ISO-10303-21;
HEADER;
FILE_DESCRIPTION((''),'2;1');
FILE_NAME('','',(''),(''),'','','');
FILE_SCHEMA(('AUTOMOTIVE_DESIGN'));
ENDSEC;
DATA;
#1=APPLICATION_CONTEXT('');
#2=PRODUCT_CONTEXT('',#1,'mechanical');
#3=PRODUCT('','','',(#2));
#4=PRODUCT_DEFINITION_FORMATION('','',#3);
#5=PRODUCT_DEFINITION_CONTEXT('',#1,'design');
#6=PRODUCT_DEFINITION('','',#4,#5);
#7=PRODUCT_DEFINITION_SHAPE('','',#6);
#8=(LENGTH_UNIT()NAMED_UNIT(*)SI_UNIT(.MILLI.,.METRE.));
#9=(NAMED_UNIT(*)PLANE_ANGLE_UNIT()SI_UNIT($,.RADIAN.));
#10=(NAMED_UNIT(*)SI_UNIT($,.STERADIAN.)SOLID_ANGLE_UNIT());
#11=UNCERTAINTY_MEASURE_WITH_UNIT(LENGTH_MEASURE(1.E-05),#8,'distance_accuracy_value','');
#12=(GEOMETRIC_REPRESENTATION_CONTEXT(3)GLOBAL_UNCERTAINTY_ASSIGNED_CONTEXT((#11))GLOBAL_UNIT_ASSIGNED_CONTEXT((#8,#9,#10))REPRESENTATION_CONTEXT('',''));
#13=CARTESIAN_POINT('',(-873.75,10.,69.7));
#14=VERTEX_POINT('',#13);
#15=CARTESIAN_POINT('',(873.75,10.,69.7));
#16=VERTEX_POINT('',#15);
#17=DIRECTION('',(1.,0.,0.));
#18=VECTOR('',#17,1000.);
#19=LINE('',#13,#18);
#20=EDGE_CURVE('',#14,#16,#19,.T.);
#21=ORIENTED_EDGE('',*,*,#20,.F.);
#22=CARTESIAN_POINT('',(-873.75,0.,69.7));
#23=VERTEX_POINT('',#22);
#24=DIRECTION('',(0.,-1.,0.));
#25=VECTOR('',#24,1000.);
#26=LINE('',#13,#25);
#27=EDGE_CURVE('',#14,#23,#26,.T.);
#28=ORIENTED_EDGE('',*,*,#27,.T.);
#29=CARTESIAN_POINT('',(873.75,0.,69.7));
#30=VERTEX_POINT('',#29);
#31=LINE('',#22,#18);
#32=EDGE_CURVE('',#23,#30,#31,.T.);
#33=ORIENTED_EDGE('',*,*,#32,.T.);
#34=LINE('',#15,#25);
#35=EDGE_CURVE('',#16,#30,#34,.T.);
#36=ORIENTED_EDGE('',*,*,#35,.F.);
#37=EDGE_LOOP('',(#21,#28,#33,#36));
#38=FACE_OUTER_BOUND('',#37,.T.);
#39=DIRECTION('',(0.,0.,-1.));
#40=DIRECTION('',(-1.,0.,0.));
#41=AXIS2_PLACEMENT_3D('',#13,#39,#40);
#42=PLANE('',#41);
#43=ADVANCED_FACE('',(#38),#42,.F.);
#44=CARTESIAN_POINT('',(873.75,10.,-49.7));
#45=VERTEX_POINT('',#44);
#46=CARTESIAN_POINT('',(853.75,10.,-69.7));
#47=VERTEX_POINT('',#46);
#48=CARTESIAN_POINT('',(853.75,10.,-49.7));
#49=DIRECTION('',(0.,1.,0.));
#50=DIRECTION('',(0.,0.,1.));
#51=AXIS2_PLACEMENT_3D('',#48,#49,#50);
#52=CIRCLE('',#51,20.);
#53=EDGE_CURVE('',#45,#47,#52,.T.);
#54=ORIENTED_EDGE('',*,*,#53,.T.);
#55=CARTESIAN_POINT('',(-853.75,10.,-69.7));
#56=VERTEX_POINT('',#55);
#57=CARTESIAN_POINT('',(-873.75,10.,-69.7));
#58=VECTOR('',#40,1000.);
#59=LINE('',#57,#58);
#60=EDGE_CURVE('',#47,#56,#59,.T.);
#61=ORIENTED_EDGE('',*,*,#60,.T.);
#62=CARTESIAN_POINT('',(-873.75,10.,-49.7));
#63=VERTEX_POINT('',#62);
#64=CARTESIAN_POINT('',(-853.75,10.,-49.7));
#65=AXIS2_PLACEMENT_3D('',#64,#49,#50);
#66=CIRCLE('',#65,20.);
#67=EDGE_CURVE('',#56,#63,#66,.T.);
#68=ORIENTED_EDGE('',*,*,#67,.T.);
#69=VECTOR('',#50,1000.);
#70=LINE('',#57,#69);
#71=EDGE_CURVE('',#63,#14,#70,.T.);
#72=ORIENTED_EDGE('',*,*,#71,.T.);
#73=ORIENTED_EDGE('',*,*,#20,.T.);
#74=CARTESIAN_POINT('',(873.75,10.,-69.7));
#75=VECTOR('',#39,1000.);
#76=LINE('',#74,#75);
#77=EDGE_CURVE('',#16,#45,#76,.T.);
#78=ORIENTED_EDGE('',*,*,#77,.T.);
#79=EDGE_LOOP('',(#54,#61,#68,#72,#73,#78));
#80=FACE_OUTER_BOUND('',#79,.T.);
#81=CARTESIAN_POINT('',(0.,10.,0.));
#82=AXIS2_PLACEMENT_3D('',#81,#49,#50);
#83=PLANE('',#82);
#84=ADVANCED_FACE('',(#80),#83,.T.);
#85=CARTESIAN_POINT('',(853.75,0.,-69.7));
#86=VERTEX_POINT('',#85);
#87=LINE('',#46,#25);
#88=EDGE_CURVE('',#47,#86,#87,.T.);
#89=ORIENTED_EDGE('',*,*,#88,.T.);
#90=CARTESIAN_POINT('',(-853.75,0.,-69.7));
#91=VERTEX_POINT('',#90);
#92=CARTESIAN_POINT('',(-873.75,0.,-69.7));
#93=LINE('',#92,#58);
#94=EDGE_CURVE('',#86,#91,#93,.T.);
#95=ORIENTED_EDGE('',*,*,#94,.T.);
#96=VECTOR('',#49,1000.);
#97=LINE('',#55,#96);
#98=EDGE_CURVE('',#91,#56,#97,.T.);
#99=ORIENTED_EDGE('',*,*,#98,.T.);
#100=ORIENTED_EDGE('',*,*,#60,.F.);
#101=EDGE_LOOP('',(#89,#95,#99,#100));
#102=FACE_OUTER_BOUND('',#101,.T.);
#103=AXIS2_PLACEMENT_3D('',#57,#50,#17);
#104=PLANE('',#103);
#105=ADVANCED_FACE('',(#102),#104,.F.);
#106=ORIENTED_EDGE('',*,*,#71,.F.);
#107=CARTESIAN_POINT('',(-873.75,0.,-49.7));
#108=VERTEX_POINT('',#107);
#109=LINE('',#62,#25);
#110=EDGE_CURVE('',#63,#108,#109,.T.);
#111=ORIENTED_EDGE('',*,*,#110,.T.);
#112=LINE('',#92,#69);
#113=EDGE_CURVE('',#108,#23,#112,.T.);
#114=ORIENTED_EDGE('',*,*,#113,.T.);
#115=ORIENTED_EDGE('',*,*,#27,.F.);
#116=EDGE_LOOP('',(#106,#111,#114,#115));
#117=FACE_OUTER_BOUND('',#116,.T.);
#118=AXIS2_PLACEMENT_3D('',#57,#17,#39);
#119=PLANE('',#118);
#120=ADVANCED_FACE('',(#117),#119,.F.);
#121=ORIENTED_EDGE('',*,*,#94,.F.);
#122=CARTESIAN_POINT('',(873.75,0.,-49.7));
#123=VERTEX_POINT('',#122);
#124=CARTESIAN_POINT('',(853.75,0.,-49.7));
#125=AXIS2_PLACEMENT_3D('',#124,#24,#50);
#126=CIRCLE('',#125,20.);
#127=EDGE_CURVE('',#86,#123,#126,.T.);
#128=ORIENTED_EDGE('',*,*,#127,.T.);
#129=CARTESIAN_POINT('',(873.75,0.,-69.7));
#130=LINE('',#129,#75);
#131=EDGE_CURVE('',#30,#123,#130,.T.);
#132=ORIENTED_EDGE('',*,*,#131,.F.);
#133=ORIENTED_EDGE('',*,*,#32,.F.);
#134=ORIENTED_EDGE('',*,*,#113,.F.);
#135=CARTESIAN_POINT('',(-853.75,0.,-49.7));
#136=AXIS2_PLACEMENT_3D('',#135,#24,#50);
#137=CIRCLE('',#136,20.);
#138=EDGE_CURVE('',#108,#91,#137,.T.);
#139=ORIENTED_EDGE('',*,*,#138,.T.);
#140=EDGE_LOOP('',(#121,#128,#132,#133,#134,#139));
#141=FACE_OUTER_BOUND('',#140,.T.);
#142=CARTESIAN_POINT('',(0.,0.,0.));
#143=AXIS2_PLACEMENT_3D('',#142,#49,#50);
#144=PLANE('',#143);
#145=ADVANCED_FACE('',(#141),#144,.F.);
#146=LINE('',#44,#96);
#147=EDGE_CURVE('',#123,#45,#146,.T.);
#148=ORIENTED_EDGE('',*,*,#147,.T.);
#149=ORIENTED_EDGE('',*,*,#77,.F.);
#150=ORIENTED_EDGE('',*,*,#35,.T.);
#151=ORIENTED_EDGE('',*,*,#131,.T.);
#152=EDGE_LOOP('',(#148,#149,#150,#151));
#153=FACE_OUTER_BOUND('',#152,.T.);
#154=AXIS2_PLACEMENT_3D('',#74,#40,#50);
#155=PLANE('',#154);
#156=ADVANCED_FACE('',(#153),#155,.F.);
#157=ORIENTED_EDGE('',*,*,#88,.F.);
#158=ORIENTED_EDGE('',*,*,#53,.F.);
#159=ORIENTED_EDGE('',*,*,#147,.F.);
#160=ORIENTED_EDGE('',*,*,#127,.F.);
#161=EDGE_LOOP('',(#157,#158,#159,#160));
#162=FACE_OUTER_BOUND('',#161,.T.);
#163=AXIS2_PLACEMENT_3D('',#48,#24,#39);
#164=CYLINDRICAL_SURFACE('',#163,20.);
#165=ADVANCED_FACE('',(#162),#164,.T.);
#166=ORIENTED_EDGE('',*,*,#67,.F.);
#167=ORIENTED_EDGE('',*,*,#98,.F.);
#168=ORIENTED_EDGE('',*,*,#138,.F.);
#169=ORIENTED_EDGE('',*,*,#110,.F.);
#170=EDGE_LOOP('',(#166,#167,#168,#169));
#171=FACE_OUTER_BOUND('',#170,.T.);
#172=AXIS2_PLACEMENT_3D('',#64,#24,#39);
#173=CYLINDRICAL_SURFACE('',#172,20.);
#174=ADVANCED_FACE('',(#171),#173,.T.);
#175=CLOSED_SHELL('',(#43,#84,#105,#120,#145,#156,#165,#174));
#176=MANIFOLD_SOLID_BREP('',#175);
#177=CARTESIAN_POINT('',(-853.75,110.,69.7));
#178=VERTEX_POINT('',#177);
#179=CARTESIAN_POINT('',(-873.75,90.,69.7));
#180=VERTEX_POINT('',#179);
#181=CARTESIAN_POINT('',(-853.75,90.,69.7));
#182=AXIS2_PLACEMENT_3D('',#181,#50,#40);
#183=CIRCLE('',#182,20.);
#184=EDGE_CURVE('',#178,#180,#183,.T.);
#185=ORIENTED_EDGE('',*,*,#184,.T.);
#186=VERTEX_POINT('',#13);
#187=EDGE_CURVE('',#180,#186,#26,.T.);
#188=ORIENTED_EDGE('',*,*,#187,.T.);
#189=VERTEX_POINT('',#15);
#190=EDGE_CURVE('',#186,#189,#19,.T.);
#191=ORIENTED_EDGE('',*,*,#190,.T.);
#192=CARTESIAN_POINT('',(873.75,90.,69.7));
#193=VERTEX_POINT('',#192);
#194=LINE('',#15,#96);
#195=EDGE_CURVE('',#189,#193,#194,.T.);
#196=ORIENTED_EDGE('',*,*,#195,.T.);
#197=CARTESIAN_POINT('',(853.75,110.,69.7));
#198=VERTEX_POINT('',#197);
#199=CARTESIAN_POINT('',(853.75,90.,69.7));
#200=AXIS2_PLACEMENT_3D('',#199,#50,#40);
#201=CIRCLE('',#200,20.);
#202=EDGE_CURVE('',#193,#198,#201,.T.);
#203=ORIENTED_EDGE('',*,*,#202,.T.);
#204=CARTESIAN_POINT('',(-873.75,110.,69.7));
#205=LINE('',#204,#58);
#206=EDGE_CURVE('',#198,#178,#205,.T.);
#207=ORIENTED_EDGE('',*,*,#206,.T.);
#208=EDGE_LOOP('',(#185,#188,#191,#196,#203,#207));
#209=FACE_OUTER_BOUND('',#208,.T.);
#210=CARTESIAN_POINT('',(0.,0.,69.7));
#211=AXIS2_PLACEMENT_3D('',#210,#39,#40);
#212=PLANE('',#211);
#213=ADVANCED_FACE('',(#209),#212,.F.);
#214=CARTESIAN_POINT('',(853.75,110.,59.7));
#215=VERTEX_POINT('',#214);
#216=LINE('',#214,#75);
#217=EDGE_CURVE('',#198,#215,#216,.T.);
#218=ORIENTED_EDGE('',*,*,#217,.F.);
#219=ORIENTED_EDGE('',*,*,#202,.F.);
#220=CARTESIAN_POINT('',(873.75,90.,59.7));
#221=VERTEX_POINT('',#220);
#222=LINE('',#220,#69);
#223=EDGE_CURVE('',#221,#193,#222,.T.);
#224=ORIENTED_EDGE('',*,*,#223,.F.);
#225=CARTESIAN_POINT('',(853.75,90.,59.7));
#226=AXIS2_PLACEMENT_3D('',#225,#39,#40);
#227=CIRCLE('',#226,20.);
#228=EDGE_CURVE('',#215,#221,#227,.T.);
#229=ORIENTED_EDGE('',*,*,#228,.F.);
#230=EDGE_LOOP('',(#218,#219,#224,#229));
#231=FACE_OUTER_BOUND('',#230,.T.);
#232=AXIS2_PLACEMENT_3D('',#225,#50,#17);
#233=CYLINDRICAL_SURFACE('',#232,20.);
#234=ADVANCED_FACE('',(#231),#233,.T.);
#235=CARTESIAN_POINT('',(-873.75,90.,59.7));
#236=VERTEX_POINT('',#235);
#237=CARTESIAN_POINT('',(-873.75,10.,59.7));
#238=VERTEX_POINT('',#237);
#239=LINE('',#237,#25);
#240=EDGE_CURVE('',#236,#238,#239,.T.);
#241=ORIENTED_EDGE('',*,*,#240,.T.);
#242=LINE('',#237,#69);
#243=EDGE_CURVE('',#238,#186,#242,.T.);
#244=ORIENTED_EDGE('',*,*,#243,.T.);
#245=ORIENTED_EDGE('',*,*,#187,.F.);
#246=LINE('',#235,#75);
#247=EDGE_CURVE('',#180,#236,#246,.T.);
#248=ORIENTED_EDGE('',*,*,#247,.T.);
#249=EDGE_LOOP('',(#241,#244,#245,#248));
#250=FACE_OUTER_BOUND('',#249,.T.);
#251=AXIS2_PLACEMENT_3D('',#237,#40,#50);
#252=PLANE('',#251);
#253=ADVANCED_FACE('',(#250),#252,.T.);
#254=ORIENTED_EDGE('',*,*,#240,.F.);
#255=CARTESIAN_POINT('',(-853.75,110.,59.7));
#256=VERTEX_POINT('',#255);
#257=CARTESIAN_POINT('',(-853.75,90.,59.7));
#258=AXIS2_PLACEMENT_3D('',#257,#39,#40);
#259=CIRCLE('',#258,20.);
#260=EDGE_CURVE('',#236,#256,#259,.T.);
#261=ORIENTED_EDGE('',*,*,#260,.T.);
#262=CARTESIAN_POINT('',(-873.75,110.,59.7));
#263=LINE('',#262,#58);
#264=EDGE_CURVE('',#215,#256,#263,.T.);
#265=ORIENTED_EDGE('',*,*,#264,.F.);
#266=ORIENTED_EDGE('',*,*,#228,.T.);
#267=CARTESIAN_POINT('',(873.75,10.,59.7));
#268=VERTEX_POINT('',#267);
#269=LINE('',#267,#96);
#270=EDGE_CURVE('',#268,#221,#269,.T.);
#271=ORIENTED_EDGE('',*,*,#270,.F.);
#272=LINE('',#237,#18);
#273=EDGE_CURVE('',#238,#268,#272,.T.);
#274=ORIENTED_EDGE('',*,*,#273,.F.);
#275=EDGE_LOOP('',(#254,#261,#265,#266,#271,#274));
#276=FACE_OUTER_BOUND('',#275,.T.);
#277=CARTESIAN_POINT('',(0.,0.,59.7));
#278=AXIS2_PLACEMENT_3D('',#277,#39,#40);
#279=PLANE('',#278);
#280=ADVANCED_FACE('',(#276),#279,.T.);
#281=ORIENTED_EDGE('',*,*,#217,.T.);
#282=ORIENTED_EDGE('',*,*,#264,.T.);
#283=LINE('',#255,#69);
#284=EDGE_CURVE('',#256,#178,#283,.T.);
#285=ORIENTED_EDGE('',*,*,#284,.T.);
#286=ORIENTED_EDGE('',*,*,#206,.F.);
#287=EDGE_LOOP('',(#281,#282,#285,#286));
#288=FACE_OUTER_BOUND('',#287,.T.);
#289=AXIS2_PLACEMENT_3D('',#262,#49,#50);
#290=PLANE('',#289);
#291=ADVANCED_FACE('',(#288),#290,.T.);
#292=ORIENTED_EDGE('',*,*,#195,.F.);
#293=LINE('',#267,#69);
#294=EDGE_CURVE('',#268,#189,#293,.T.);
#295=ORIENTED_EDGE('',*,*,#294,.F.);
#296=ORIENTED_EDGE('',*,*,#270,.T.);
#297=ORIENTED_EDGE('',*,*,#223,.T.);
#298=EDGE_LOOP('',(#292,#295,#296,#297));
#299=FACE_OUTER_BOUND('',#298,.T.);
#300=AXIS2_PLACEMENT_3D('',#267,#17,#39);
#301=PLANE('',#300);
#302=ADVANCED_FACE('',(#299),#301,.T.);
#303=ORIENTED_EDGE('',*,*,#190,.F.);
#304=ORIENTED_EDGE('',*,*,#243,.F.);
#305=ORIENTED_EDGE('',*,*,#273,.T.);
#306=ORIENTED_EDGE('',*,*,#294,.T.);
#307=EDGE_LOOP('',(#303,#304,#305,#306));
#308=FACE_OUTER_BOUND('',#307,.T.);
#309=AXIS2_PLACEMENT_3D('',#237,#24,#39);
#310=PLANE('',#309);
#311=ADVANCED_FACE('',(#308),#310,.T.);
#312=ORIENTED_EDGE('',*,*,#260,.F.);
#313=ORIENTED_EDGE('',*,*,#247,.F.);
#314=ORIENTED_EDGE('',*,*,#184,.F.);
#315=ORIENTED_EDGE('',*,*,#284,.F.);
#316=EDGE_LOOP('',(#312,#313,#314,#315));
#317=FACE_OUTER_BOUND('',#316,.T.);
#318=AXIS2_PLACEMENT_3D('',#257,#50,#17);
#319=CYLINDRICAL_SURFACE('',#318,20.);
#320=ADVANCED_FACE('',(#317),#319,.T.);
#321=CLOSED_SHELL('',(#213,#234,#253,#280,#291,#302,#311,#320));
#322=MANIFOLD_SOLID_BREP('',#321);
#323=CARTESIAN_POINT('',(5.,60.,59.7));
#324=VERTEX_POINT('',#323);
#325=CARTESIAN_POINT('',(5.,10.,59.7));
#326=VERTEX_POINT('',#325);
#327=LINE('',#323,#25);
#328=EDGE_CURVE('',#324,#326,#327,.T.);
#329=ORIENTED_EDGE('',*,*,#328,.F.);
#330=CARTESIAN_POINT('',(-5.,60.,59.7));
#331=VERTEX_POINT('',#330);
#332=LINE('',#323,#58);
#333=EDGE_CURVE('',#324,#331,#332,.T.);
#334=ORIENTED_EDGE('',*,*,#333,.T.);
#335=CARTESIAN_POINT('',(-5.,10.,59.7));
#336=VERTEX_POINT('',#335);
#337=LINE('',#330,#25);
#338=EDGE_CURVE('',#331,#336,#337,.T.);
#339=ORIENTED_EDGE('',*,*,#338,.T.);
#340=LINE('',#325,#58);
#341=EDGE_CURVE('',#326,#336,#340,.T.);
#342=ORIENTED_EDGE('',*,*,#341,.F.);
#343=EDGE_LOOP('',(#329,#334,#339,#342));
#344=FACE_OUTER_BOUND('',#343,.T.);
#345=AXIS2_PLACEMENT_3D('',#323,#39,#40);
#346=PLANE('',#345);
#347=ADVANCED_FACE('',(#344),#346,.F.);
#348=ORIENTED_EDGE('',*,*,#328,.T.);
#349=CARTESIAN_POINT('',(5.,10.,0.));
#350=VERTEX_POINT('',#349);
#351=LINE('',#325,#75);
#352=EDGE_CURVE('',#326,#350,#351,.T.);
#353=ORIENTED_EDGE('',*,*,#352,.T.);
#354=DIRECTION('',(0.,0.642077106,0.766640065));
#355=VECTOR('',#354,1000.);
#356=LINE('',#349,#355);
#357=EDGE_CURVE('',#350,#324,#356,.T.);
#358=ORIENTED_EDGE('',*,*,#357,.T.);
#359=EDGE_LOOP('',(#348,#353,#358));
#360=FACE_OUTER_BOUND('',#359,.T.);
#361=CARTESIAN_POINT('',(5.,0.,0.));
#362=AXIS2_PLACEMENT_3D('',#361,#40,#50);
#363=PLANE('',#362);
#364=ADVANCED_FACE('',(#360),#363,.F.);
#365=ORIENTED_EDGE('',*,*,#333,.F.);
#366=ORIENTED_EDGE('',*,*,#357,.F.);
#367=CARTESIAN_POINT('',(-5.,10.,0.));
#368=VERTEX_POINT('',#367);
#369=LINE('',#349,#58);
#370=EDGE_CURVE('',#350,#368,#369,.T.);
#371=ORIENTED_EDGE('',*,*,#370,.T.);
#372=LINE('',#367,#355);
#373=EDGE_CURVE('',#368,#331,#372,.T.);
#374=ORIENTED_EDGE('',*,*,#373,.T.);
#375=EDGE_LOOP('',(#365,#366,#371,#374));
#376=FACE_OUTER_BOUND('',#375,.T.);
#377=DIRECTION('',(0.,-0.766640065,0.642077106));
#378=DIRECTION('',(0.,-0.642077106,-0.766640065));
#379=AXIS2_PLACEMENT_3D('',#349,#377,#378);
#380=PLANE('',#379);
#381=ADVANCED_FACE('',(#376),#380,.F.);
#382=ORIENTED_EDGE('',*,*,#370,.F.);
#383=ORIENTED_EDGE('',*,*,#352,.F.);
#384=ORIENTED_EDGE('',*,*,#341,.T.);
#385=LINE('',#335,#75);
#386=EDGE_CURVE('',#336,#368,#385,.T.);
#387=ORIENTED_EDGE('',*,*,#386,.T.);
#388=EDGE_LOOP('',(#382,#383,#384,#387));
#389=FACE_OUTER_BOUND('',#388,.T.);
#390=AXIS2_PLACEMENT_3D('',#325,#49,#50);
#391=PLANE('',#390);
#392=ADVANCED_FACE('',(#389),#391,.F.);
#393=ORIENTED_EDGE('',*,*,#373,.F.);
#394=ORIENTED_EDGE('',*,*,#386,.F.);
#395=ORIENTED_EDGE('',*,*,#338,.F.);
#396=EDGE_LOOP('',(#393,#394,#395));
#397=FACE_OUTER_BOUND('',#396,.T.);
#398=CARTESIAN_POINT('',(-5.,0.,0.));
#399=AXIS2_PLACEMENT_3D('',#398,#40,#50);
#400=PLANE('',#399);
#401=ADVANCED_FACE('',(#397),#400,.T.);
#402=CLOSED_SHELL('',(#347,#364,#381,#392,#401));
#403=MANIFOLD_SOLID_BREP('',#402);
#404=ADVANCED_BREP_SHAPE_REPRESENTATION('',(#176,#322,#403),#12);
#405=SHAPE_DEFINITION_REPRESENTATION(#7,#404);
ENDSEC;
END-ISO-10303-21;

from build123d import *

# Parameters (mm, degrees)
SKETCH_1_W      = 1747.5
SKETCH_1_H      = 139.4
EXTRUDE_1_DEPTH = 10
SKETCH_2_W      = 1747.5
SKETCH_2_H      = 100
EXTRUDE_2_DEPTH = 10
EXTRUDE_3_DEPTH = 5
FILLET_1_R      = 20
FILLET_2_R      = 20


with BuildPart() as part:
    # 草图1 → 凸台-拉伸1 (new body)
    with BuildSketch(Plane(origin=(0, 0, 0), x_dir=(1, 0, 0), z_dir=(0, 1, 0))):
        Rectangle(SKETCH_1_W, SKETCH_1_H)
    extrude(amount=EXTRUDE_1_DEPTH)

    # 圆角2
    fillet_2_edges = [part.edges().sort_by_distance(p)[0] for p in [
        (-873.75, 5, -69.7),
        (873.75, 5, -69.7),
    ]]
    fillet(fillet_2_edges, radius=FILLET_2_R)


with BuildPart() as body_2:
    # 草图2 → 凸台-拉伸2 (new body)
    with BuildSketch(Plane.XY.offset(69.7)):
        with Locations((0, 60)):
            Rectangle(SKETCH_2_W, SKETCH_2_H)
    extrude(amount=-EXTRUDE_2_DEPTH)

    # 圆角1
    fillet_1_edges = [body_2.edges().sort_by_distance(p)[0] for p in [
        (-873.75, 110, 64.7),
        (873.75, 110, 64.7),
    ]]
    fillet(fillet_1_edges, radius=FILLET_1_R)


with BuildPart() as body_3:
    # 草图3 → 凸台-拉伸3 (new, symmetric)
    with BuildSketch(Plane(origin=(0, 0, 0), x_dir=(0, 0, -1), z_dir=(1, 0, 0))):
        Polygon((0, 10), (-59.7, 60), (-59.7, 10), align=None)
    extrude(amount=EXTRUDE_3_DEPTH, both=True)


solid = Compound([part.part, body_2.part, body_3.part])
